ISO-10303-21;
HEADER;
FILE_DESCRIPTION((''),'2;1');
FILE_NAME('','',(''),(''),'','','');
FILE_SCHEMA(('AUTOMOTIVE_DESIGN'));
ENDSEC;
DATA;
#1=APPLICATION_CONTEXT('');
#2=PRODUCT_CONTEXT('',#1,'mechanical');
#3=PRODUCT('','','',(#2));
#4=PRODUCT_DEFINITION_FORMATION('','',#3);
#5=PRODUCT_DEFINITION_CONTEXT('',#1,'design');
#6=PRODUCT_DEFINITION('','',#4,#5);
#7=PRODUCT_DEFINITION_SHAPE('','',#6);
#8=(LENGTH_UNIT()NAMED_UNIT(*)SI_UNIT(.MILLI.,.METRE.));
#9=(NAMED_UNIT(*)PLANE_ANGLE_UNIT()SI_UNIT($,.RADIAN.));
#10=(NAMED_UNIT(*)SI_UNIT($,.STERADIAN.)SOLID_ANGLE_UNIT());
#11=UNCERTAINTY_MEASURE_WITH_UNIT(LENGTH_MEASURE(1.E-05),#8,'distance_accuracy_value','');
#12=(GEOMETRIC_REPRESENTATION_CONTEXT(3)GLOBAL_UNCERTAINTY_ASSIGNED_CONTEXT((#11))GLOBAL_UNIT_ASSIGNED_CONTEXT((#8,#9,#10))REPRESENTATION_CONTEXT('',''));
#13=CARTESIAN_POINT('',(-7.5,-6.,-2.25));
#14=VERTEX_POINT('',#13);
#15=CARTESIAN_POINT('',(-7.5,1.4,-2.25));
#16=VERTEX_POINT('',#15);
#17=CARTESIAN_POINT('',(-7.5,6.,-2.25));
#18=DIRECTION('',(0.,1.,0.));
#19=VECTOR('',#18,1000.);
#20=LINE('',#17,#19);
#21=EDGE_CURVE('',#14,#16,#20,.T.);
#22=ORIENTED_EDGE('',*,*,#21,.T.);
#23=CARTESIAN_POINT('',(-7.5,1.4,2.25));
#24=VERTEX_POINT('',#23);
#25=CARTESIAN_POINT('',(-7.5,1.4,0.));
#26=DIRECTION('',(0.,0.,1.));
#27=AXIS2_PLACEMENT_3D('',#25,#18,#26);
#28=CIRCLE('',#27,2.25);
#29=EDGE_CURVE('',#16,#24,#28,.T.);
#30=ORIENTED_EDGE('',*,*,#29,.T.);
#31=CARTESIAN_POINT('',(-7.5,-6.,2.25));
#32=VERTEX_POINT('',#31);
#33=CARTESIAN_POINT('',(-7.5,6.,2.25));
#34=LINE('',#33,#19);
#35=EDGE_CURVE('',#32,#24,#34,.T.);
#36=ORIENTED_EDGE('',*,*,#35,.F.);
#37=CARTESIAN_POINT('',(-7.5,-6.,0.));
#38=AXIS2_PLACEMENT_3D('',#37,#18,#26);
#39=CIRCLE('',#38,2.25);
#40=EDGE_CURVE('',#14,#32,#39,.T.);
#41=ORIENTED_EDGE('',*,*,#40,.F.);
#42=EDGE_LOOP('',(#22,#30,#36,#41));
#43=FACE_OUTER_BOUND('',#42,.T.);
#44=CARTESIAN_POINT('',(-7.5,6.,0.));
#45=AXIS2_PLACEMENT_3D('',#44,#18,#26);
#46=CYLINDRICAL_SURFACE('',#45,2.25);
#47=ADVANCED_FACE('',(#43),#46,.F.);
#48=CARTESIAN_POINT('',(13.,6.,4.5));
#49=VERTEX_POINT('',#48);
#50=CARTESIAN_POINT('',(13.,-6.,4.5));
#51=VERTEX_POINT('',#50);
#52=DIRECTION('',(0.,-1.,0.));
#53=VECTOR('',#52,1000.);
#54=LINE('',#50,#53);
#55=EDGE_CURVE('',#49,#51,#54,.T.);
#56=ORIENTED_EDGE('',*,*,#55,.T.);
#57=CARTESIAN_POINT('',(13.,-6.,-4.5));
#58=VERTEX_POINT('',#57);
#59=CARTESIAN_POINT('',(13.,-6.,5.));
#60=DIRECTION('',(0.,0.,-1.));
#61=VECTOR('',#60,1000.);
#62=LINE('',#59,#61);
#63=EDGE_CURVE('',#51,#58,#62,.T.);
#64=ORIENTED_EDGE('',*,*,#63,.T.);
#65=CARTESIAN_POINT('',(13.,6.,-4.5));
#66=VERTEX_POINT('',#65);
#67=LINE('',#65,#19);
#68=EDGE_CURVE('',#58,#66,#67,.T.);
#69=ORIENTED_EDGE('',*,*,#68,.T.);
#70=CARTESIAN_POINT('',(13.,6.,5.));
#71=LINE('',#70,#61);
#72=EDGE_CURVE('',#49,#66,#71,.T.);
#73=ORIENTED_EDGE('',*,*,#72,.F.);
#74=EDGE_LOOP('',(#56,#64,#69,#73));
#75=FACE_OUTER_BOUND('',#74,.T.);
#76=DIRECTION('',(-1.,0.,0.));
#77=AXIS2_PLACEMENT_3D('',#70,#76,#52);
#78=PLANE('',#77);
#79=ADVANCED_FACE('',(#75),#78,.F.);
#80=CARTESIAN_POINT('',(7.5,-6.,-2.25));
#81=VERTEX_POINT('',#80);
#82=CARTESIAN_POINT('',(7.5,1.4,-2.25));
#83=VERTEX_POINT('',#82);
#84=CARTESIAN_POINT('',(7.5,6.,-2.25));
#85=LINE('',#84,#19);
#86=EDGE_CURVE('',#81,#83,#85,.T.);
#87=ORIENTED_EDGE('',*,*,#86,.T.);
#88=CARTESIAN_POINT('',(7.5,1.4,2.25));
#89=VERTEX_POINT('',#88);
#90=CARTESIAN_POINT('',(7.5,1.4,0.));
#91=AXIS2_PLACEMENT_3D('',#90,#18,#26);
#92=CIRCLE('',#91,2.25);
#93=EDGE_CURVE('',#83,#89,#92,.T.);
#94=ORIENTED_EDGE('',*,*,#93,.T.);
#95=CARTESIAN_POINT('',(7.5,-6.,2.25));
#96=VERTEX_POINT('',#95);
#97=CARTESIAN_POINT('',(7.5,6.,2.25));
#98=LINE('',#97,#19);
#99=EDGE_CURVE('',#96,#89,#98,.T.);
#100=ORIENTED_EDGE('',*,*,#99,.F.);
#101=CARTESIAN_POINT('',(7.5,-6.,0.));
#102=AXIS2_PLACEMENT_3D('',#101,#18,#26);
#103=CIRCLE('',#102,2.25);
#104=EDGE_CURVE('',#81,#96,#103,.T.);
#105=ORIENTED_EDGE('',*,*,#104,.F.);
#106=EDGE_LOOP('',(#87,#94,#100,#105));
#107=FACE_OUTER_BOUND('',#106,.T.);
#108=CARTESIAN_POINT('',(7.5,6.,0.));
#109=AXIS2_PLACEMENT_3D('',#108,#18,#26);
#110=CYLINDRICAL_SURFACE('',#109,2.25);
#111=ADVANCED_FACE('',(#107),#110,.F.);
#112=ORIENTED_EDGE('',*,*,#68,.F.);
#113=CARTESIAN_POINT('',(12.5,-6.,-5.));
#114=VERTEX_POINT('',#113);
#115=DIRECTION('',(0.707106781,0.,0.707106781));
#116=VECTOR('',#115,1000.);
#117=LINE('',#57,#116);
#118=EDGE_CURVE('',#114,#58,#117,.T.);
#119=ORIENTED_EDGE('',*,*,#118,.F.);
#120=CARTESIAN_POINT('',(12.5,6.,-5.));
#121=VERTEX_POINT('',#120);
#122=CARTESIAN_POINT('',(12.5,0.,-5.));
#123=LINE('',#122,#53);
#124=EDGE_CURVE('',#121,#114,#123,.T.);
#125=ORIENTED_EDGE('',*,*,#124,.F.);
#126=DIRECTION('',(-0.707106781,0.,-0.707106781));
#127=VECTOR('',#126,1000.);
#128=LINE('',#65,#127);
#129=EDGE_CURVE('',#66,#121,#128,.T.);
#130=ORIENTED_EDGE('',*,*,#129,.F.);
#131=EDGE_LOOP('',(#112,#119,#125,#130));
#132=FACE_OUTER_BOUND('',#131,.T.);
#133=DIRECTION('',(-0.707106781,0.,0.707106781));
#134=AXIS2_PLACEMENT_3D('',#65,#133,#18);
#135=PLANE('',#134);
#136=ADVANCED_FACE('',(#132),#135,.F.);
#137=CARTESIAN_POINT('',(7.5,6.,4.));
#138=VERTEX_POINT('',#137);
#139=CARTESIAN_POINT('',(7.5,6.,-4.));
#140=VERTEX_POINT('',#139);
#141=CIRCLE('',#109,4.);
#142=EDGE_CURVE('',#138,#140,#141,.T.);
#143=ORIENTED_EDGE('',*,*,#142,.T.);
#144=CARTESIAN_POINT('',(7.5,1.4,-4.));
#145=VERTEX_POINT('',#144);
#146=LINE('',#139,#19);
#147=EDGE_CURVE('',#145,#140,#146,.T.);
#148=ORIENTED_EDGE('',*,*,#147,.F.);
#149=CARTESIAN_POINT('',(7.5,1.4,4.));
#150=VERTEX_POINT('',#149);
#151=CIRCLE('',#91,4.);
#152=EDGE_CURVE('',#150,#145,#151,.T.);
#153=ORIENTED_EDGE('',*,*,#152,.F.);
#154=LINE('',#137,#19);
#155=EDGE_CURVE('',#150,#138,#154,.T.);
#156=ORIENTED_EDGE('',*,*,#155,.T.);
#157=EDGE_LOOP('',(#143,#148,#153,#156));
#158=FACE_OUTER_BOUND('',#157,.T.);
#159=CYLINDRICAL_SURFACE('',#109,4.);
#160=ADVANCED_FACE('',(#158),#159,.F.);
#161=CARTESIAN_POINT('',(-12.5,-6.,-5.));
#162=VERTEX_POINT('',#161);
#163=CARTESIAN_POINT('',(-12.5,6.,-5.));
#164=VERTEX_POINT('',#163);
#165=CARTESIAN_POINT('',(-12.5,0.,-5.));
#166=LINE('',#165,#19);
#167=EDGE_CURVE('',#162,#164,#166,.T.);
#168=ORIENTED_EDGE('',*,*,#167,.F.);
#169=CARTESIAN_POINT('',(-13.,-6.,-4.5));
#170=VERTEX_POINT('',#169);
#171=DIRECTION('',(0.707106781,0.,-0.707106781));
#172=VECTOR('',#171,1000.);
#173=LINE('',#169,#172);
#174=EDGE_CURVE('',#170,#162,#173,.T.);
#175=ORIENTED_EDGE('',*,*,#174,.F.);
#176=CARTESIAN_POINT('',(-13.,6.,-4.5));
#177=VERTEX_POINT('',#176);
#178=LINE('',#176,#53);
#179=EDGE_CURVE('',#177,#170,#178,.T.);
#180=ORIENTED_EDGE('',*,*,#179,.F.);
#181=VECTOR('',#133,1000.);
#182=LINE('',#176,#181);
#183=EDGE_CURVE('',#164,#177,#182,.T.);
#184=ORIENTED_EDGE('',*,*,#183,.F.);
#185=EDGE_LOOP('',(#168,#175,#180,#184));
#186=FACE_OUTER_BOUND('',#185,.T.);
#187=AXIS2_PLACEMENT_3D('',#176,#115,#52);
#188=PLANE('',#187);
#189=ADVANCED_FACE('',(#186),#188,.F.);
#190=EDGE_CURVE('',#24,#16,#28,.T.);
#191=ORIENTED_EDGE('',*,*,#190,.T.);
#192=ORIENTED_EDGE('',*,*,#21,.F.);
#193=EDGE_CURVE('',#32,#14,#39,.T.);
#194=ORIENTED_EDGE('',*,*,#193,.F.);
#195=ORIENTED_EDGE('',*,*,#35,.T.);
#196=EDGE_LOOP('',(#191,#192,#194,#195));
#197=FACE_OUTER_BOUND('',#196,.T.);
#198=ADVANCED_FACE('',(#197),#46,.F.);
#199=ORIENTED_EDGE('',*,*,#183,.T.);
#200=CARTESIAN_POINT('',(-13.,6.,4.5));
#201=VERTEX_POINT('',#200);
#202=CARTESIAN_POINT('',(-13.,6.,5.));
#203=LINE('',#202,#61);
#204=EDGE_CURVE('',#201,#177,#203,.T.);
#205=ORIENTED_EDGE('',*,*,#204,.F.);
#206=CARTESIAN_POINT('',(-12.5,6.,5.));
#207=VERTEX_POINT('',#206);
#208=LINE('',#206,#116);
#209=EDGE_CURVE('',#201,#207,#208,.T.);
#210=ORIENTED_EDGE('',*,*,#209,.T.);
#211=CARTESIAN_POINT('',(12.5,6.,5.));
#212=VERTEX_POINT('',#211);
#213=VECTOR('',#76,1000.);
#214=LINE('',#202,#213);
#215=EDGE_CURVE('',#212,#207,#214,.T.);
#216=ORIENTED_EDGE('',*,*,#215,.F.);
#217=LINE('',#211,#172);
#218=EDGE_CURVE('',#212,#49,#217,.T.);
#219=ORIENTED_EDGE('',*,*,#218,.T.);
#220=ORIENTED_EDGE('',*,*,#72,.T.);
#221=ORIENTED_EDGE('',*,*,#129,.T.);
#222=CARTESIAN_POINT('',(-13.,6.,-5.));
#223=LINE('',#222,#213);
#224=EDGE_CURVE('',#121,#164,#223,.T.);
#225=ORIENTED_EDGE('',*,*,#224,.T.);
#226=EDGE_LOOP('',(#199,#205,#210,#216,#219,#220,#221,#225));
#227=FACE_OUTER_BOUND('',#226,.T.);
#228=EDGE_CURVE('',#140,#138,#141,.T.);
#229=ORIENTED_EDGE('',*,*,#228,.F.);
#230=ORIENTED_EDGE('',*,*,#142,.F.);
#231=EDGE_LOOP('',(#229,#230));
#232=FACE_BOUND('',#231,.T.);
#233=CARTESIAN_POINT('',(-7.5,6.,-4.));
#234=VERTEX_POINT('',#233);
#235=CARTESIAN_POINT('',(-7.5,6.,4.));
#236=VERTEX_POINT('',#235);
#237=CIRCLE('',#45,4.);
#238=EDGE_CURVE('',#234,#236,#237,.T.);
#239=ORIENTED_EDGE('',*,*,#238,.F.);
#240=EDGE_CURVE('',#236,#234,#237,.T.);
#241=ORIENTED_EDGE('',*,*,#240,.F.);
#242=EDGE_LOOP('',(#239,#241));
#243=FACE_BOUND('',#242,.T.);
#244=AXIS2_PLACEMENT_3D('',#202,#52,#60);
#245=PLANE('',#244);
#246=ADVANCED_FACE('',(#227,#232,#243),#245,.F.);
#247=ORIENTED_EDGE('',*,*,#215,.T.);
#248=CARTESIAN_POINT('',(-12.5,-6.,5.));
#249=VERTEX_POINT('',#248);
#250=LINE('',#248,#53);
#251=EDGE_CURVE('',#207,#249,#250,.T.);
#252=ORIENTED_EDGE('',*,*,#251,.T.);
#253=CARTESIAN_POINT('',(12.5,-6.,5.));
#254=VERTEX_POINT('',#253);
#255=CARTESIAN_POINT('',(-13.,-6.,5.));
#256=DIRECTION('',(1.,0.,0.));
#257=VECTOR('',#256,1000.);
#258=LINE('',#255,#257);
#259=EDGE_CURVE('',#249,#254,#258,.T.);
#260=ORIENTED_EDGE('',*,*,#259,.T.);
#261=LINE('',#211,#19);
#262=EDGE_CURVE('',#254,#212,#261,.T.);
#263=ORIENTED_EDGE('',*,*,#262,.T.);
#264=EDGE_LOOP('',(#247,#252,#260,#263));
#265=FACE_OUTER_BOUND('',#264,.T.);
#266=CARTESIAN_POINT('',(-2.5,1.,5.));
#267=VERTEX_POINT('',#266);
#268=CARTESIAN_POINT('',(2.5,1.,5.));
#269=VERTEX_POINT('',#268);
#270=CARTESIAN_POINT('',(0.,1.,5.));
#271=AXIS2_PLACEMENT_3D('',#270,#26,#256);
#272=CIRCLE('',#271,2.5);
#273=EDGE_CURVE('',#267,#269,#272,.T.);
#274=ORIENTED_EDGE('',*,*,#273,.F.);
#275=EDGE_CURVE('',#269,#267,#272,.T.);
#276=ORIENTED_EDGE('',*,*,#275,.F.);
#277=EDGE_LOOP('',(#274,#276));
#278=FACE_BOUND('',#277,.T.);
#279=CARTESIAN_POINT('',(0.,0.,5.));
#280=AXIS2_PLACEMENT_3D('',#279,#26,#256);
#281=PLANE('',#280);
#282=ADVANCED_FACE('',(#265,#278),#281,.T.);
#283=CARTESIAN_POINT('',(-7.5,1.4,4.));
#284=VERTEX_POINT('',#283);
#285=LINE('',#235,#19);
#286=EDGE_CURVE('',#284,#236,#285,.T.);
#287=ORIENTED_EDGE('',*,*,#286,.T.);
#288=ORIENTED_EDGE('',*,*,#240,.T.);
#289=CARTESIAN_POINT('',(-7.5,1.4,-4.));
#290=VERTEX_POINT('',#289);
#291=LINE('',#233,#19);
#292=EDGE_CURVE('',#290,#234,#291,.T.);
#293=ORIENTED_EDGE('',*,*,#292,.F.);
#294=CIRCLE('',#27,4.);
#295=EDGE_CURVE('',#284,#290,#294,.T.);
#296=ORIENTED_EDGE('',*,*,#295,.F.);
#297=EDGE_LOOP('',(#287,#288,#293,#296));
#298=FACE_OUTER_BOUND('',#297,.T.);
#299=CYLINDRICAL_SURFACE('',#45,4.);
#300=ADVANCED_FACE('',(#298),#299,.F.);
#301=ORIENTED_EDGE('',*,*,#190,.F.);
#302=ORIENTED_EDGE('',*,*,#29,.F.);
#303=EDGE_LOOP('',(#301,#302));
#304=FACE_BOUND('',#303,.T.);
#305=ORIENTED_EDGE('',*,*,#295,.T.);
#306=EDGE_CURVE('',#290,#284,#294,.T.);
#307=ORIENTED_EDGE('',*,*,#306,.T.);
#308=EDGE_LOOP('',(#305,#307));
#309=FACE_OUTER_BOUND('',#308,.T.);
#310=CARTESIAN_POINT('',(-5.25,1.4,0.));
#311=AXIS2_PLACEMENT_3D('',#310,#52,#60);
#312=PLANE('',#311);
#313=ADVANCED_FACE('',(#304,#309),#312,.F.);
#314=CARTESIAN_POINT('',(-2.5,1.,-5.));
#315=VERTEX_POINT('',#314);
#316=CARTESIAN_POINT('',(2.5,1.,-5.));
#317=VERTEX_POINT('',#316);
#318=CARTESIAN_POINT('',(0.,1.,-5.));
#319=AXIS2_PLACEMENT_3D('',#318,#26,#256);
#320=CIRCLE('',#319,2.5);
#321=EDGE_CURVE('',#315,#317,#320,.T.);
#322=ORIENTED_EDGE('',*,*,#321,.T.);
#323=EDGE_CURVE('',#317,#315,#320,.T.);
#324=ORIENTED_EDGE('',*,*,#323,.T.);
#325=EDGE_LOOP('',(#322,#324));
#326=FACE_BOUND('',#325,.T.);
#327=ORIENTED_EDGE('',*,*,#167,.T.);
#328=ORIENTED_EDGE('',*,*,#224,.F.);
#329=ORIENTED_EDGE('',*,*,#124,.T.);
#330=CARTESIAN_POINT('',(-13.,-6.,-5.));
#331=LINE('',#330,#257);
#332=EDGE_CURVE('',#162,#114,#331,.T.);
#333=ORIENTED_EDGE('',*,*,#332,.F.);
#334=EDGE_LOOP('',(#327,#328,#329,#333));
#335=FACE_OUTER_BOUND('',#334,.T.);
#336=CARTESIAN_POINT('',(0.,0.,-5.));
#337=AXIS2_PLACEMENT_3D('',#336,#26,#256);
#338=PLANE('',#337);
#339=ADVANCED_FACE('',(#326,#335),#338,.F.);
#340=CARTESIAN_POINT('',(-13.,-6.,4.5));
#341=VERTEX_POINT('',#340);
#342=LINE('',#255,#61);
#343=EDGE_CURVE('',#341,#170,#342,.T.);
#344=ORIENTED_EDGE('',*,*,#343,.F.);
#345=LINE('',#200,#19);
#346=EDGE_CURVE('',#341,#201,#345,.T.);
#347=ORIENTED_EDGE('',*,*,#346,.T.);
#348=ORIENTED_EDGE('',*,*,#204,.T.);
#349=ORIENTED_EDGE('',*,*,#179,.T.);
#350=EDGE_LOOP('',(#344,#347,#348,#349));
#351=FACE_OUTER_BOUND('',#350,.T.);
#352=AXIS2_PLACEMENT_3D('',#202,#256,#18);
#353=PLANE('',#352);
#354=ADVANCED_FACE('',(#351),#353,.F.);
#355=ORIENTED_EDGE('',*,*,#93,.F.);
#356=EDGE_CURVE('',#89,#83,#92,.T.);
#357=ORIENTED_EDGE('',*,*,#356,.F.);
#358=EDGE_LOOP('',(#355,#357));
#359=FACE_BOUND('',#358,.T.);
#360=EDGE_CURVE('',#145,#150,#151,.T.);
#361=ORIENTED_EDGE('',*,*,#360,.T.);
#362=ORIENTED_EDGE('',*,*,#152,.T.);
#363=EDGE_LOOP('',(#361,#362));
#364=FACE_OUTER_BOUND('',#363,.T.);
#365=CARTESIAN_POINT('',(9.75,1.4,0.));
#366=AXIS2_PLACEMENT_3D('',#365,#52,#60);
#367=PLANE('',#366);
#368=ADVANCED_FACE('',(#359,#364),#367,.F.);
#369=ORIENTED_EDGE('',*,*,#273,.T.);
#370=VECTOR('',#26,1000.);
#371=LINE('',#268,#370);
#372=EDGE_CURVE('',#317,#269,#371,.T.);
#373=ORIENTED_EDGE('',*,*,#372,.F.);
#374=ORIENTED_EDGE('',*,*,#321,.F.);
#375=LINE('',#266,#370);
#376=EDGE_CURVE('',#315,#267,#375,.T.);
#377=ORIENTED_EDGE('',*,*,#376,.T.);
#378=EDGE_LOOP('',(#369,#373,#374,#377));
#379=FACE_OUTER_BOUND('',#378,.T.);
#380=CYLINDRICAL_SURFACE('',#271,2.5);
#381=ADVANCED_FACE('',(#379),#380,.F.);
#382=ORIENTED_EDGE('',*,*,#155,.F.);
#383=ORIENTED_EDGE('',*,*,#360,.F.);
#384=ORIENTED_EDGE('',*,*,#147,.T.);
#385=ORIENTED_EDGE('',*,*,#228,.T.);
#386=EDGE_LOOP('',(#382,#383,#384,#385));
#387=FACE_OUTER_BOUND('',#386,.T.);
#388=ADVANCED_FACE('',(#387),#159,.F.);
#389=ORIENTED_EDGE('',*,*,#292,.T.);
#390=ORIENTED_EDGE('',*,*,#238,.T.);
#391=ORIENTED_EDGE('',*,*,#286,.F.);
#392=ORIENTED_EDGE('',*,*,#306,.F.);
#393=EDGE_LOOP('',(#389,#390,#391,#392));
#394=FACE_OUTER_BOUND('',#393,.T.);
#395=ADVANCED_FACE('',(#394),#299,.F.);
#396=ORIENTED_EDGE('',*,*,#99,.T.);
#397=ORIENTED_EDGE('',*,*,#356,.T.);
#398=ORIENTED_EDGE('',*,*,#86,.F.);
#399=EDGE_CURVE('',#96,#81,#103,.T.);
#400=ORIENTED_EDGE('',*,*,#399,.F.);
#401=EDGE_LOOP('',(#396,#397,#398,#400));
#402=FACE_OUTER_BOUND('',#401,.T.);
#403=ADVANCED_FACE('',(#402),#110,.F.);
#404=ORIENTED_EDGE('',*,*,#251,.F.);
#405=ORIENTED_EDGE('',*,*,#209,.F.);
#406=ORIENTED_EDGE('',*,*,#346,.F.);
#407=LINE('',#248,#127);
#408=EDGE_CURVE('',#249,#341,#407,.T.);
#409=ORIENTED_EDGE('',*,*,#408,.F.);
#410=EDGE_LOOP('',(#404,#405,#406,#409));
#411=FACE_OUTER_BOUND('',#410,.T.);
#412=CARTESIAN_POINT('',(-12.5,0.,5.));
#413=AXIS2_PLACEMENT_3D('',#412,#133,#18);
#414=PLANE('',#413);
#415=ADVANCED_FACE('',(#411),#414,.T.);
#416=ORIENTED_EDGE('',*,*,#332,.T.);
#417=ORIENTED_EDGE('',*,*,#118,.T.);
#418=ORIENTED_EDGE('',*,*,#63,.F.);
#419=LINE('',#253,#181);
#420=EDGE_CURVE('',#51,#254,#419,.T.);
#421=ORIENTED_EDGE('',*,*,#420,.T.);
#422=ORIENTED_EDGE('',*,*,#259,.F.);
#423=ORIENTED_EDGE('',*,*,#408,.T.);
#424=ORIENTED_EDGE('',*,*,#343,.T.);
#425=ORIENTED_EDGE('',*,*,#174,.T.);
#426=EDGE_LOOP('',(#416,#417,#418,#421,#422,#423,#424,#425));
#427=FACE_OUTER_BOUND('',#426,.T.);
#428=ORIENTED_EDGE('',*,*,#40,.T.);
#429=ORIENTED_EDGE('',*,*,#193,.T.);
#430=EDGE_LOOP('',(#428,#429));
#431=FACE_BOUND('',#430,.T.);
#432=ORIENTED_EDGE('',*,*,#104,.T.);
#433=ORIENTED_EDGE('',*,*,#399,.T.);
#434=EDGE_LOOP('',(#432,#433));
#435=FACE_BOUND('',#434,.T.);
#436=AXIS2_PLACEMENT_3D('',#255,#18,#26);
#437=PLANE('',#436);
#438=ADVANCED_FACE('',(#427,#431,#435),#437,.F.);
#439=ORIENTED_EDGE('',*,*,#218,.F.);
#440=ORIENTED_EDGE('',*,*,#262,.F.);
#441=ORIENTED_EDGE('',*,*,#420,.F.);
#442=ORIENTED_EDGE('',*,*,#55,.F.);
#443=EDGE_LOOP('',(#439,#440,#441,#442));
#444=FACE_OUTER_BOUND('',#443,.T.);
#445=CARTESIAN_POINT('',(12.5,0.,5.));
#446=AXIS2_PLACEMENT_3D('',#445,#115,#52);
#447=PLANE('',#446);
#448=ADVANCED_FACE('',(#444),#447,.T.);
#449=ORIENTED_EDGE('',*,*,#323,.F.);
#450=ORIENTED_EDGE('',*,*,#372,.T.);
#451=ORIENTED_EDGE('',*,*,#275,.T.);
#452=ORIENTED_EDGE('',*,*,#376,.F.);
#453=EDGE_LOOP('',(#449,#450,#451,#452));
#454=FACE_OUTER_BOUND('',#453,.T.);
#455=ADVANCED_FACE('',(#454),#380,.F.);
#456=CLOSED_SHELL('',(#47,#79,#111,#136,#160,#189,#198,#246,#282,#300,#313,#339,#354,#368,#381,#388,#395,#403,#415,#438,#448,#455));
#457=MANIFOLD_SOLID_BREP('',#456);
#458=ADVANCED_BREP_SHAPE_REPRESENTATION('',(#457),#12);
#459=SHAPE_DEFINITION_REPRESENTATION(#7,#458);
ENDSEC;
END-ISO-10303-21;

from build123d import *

# Parameters (mm, degrees)
SKETCH_1_W                = 26
SKETCH_1_H                = 12
EXTRUDE_1_DEPTH           = 5
HOLE_WIZARD_1_D           = 4.5
HOLE_WIZARD_1_CBORE_D     = 8
HOLE_WIZARD_1_CBORE_DEPTH = 4.6
HOLE_WIZARD_M6_1_D        = 5
CHAMFER_1_SIZE            = 0.5


with BuildPart() as part:
    # 草图1 → 凸台-拉伸1 (new, symmetric)
    with BuildSketch(Plane.XY):
        Rectangle(SKETCH_1_W, SKETCH_1_H)
    extrude(amount=EXTRUDE_1_DEPTH, both=True)

    # 打孔尺寸(%根据)内六角圆柱头螺钉的类型1 (through all)
    with Locations(Plane(origin=(0, 6, 0), x_dir=(1, 0, 0), z_dir=(0, 1, 0))):
        with Locations((-7.5, 0), (7.5, 0)):
            CounterBoreHole(HOLE_WIZARD_1_D / 2, HOLE_WIZARD_1_CBORE_D / 2, HOLE_WIZARD_1_CBORE_DEPTH)

    # M6 螺纹孔1 (through all)
    with Locations(Plane.XY.offset(5)):
        with Locations((0, 1)):
            Hole(HOLE_WIZARD_M6_1_D / 2)

    # 倒角1
    chamfer_1_edges = [part.edges().sort_by_distance(p)[0] for p in [
        (-13, 0, 5),
        (13, 0, 5),
        (-13, 0, -5),
        (13, 0, -5),
    ]]
    chamfer(chamfer_1_edges, length=CHAMFER_1_SIZE)


solid = part.part
